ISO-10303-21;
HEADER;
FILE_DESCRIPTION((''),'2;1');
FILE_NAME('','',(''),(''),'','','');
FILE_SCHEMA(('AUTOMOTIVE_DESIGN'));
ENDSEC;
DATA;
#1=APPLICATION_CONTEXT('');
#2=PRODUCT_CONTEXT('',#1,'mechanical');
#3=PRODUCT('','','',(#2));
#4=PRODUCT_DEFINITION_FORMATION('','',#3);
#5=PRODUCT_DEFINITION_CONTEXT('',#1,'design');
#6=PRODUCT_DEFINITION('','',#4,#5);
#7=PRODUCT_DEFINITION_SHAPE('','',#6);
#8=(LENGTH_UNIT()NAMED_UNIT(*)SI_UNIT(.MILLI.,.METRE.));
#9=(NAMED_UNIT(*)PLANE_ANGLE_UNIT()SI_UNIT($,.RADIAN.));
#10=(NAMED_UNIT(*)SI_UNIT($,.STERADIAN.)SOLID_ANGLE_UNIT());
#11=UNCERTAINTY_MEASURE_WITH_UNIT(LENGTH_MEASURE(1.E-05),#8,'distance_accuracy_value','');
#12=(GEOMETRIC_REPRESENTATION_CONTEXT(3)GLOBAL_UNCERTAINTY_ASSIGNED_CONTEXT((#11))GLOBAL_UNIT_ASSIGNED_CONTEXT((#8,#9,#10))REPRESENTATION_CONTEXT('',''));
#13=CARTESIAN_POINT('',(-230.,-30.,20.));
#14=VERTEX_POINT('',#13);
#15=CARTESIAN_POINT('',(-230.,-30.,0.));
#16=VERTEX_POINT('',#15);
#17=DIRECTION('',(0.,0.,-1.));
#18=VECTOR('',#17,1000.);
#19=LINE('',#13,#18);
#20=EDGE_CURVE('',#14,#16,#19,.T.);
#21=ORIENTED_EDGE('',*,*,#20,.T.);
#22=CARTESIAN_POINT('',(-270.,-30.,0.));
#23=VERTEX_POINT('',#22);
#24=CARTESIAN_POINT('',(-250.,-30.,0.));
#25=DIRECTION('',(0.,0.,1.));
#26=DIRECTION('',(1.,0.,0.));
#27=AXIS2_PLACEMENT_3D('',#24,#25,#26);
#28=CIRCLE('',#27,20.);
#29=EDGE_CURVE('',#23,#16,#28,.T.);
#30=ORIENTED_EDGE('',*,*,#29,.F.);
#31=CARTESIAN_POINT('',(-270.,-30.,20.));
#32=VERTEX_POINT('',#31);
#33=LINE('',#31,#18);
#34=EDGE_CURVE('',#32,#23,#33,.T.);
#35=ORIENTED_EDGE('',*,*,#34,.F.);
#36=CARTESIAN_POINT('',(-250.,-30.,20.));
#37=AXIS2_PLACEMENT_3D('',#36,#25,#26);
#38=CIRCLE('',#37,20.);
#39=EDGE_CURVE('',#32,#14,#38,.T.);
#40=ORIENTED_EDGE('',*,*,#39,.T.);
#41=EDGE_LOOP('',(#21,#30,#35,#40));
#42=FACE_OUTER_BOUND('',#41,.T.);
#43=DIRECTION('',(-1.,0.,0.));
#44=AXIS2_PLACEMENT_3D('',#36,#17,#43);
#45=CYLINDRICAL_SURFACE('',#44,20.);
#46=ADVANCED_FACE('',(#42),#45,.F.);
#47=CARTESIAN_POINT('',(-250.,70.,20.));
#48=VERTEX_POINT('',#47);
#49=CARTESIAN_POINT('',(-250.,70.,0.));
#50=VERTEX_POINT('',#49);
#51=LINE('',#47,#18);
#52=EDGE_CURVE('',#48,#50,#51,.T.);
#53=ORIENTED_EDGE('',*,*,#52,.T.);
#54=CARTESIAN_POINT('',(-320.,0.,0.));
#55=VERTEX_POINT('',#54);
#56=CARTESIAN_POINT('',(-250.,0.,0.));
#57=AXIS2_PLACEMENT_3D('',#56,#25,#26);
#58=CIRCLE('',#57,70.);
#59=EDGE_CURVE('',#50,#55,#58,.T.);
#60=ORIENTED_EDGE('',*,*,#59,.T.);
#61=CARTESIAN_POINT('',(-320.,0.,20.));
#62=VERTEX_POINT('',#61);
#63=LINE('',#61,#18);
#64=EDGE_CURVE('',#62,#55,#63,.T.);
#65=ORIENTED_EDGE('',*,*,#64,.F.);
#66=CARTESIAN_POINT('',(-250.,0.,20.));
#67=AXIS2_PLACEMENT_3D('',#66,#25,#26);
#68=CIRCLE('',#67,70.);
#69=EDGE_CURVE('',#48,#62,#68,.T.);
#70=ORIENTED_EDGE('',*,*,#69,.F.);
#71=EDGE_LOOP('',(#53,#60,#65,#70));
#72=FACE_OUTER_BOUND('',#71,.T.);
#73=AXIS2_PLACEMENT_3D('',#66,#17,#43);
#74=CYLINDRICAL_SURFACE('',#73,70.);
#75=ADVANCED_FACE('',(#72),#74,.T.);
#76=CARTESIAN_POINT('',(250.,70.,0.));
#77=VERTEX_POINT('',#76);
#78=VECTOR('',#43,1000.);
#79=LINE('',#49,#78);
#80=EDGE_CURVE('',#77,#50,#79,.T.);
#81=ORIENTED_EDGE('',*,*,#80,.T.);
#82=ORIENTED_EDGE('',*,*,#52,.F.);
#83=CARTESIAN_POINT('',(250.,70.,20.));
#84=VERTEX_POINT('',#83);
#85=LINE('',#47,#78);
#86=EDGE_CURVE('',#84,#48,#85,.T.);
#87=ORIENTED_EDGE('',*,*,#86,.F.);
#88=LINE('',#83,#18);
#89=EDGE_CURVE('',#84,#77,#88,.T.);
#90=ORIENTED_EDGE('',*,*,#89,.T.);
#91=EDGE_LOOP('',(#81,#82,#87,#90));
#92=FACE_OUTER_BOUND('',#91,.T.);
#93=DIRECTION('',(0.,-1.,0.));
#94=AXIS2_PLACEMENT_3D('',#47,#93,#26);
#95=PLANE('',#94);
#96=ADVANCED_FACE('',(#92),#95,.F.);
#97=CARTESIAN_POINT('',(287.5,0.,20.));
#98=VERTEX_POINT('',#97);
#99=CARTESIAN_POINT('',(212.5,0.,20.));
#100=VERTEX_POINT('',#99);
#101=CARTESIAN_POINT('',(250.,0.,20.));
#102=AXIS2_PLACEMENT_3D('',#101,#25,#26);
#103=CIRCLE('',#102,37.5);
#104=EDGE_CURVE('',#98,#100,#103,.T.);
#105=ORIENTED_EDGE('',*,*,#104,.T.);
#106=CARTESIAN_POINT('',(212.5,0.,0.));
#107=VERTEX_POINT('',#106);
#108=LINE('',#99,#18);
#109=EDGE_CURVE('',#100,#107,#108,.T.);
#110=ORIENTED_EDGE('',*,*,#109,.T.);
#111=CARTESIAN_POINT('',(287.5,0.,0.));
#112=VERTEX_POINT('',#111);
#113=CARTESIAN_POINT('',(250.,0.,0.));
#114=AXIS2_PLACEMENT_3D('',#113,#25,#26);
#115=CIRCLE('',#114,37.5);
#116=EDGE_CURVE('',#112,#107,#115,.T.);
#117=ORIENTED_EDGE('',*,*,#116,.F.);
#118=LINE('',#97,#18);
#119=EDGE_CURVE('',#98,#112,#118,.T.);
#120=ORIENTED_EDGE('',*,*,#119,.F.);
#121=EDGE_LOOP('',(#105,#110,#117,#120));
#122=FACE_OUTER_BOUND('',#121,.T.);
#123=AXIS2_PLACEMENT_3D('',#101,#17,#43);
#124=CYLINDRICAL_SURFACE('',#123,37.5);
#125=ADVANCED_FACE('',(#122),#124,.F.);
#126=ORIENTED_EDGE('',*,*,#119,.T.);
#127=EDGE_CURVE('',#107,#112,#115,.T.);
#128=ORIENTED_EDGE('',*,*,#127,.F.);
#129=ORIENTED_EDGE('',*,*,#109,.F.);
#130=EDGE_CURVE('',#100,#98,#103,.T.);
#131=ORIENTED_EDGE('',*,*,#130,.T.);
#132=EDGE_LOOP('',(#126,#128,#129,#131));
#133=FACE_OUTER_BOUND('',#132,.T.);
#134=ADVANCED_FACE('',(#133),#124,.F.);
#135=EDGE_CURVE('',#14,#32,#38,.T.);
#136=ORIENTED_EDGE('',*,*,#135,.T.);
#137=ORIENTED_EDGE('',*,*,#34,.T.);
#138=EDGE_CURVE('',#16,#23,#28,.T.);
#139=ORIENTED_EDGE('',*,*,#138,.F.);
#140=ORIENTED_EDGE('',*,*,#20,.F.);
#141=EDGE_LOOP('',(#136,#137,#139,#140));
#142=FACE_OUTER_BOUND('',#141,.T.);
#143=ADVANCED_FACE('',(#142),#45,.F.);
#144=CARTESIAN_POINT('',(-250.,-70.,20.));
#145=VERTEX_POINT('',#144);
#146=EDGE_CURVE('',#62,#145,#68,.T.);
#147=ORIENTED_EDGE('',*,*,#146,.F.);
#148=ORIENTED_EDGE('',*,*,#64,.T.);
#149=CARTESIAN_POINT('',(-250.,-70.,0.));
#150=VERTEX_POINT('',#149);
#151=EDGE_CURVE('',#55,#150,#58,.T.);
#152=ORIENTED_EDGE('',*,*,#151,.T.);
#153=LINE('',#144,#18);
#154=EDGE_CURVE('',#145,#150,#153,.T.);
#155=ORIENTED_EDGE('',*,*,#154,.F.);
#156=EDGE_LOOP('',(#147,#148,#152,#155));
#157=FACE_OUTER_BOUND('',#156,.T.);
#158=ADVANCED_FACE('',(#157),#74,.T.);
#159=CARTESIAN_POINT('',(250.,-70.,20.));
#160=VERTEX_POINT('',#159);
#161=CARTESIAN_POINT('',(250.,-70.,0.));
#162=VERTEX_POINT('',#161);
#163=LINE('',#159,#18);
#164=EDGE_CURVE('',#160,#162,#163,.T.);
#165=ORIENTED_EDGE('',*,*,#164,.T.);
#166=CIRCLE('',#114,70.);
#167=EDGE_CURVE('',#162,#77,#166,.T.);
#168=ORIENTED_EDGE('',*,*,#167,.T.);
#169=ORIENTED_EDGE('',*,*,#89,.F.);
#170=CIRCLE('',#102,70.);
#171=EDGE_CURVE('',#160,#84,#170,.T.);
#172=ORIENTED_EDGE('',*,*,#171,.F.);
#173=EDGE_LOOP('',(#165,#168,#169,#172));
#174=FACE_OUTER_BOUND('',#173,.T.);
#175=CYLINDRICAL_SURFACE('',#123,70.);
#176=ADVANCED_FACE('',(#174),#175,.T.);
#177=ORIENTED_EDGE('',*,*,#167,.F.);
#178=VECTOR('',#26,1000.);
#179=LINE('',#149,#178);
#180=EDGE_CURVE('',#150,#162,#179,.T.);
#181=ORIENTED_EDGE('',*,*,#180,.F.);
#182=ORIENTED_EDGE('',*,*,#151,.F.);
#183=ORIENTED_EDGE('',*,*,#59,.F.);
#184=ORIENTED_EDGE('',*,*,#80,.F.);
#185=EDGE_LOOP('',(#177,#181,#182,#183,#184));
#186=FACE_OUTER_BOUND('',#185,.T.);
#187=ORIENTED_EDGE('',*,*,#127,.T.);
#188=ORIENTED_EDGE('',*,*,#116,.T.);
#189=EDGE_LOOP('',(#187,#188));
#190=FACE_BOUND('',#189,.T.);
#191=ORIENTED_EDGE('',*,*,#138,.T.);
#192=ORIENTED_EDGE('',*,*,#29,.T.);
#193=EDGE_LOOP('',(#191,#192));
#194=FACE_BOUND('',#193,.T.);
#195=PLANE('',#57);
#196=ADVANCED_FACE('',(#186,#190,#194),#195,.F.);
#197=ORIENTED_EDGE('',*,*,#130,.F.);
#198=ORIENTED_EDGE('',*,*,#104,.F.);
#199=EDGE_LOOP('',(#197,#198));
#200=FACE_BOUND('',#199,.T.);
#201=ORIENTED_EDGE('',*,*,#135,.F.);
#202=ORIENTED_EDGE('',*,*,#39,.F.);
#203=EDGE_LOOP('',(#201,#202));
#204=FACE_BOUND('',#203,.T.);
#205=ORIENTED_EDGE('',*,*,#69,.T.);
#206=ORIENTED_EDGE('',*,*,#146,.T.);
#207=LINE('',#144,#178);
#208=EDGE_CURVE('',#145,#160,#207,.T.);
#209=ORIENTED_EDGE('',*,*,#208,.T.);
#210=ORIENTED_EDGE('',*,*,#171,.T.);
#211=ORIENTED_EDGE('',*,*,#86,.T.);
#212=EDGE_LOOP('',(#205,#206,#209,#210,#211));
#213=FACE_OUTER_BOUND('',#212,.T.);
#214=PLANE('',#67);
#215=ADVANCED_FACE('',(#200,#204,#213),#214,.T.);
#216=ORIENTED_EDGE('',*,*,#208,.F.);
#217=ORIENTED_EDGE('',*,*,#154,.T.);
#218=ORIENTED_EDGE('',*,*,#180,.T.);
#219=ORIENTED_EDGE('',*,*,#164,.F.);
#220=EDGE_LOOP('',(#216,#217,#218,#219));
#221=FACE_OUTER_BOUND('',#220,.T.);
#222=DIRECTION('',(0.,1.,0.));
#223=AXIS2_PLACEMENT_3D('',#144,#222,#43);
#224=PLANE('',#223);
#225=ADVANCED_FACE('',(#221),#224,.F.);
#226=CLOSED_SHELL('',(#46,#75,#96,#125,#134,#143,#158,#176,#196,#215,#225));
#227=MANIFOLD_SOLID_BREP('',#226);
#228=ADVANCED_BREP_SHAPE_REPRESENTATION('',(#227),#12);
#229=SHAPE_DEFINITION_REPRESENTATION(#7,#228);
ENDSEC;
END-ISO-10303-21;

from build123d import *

# Parameters (mm, degrees)
SKETCH_1_R      = 37.5
SKETCH_1_R_2    = 20
EXTRUDE_1_DEPTH = 20


with BuildPart() as part:
    # 草图1 → 凸台-拉伸1 (new body)
    with BuildSketch(Plane.XY):
        with BuildLine():
            Line((-250, 70), (250, 70))
            ThreePointArc((250, 70), (320, 0), (250, -70))
            Line((250, -70), (-250, -70))
            ThreePointArc((-250, -70), (-320, 0), (-250, 70))
        make_face()
        with Locations((250, 0)):
            Circle(SKETCH_1_R, mode=Mode.SUBTRACT)
        with Locations((-250, -30)):
            Circle(SKETCH_1_R_2, mode=Mode.SUBTRACT)
    extrude(amount=EXTRUDE_1_DEPTH)


solid = part.part
